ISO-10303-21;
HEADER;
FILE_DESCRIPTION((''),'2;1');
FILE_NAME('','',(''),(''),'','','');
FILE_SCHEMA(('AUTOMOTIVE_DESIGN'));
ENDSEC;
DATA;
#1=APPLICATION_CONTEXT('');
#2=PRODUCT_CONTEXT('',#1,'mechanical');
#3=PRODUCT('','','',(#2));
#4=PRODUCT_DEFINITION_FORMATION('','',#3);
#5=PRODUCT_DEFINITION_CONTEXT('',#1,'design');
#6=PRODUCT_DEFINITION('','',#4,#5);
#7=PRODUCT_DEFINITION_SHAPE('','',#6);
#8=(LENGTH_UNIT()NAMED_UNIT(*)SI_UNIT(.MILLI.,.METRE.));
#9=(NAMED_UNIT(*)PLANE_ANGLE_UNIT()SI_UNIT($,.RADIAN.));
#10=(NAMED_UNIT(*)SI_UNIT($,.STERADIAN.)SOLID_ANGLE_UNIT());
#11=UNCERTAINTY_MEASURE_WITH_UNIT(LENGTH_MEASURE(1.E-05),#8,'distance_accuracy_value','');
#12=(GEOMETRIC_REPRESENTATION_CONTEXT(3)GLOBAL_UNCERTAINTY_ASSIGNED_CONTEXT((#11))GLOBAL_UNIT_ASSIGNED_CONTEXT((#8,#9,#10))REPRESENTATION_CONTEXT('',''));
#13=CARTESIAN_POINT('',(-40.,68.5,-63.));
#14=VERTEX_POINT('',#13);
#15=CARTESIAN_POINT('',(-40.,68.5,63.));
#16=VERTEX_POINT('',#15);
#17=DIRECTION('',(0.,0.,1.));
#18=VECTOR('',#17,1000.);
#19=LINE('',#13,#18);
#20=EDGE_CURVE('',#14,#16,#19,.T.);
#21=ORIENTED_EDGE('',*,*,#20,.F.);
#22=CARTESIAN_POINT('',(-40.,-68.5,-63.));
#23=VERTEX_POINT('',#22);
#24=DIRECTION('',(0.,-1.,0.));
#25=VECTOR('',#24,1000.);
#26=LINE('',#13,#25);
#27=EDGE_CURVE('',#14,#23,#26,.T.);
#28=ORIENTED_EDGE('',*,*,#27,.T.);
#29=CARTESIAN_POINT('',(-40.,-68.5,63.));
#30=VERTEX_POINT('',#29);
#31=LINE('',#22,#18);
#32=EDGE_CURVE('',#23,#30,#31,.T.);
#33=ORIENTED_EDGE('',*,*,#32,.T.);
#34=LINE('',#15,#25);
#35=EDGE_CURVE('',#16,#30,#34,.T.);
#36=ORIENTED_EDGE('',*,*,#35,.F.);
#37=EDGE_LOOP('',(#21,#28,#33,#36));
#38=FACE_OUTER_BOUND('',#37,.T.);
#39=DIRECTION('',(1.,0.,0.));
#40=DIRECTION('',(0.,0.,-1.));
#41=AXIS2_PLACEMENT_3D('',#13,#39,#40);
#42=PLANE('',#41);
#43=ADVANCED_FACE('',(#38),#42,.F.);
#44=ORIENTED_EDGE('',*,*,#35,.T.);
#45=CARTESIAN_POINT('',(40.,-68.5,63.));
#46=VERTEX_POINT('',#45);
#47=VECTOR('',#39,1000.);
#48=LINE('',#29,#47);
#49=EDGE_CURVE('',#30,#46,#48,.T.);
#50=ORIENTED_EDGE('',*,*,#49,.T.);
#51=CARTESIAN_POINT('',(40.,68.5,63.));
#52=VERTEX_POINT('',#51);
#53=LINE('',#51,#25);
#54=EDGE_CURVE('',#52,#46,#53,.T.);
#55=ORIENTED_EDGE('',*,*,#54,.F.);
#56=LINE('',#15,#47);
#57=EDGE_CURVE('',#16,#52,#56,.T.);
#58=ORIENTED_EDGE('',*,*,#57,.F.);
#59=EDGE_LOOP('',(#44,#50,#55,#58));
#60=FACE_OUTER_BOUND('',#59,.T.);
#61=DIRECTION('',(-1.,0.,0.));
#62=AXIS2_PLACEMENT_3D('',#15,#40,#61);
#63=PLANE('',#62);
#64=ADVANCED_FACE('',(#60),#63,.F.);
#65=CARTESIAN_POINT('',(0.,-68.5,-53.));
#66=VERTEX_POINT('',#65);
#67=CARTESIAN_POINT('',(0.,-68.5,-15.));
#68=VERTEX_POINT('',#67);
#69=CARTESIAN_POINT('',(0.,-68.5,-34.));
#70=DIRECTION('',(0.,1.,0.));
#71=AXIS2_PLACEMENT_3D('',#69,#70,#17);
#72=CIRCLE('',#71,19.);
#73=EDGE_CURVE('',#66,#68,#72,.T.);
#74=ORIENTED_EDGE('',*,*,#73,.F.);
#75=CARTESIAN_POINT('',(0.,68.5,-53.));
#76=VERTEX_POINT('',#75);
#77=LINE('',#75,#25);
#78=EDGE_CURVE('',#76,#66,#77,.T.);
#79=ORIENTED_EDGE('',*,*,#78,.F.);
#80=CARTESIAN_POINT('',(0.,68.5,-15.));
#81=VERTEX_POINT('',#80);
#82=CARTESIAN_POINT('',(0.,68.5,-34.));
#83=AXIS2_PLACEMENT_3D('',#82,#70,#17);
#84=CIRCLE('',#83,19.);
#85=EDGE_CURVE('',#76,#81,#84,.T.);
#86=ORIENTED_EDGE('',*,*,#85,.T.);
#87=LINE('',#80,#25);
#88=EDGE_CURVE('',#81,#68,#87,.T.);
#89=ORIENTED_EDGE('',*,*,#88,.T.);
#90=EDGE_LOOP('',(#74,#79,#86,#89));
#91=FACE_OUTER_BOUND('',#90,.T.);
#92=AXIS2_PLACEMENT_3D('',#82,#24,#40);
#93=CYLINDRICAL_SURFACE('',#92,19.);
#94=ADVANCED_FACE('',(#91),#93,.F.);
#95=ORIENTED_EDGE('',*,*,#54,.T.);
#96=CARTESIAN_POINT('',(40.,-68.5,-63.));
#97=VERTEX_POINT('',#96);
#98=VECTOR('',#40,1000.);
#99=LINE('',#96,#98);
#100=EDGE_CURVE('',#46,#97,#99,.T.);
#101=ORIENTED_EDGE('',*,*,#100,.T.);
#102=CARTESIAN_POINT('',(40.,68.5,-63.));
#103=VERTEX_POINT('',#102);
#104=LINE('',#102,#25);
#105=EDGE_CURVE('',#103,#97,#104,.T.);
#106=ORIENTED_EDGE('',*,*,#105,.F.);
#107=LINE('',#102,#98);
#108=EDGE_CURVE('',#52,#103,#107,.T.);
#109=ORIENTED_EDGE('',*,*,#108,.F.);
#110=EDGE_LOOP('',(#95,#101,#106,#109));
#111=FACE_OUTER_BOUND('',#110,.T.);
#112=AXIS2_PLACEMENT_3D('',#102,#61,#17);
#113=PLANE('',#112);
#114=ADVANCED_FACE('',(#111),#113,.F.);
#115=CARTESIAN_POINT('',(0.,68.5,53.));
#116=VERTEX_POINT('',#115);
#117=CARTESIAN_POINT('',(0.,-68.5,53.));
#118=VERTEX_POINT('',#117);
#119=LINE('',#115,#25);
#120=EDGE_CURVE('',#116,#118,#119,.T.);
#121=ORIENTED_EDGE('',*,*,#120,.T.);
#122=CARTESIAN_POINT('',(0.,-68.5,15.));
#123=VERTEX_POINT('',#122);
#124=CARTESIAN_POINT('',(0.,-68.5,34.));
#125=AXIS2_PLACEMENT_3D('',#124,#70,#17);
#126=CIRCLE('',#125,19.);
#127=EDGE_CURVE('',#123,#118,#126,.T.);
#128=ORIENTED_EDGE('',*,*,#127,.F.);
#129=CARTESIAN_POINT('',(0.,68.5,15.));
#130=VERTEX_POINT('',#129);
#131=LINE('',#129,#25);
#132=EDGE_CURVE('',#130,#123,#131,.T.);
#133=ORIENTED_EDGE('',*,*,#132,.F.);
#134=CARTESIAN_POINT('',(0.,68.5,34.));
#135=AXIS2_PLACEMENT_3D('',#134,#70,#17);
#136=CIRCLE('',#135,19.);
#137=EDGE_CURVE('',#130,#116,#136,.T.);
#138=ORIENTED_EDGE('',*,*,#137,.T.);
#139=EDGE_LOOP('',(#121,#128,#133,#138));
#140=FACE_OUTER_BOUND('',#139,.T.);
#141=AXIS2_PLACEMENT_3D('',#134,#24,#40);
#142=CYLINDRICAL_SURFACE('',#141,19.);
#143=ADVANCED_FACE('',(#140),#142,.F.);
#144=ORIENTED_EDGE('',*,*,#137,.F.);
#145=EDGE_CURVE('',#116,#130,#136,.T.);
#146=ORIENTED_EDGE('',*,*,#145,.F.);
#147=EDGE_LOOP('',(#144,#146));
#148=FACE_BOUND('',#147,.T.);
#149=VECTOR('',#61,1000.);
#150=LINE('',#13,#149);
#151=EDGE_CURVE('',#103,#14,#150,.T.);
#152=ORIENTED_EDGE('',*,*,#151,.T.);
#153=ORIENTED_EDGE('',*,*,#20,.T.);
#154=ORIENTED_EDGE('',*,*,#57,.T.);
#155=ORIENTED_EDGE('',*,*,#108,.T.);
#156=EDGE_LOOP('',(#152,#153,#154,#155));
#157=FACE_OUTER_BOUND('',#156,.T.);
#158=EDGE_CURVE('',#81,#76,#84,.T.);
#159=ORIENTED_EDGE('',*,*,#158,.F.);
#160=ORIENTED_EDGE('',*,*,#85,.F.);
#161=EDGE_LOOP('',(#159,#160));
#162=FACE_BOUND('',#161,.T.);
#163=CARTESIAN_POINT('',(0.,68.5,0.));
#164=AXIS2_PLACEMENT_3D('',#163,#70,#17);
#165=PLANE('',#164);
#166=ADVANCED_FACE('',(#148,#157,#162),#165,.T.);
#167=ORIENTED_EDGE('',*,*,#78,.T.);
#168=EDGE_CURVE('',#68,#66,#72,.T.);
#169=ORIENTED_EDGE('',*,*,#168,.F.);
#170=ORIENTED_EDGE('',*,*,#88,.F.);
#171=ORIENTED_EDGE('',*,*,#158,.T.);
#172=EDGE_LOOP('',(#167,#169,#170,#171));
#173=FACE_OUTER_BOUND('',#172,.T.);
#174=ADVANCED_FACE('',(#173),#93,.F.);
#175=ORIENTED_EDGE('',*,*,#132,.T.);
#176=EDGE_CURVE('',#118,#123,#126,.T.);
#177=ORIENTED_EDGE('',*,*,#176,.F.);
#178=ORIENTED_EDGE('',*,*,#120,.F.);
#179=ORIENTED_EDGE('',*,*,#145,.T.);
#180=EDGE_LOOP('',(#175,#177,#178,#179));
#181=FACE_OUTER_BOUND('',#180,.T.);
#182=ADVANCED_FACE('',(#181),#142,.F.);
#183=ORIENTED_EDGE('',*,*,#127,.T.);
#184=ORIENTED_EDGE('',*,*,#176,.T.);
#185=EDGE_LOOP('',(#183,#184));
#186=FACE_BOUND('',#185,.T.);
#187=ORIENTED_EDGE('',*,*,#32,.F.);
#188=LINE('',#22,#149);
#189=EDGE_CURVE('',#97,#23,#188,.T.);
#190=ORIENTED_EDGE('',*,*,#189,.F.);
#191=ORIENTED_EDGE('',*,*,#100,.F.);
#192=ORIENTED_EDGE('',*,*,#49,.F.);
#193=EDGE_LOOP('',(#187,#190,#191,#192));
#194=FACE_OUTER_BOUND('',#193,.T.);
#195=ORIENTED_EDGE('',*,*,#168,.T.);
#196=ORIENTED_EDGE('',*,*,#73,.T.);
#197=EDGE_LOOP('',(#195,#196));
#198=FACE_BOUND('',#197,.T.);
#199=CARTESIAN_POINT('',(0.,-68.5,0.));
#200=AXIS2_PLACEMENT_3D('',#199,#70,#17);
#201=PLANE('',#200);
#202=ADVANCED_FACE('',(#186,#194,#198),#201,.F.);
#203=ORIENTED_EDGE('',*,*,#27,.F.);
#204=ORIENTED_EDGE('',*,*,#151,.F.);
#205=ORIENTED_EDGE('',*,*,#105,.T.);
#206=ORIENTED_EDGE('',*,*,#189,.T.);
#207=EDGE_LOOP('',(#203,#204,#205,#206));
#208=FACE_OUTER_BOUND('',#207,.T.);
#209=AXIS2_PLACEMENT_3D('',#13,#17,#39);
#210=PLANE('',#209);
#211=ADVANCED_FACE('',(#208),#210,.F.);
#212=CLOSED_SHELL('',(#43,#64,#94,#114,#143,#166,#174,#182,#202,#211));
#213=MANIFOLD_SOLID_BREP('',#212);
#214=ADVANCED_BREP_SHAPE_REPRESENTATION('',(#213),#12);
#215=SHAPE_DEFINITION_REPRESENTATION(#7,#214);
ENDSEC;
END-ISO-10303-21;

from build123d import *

# Parameters (mm, degrees)
SKETCH2_W           = 80
SKETCH2_H           = 126
SKETCH2_R           = 19
BOSS_EXTRUDE1_DEPTH = 68.5


with BuildPart() as part:
    # Sketch2 → Boss-Extrude1 (new, symmetric)
    with BuildSketch(Plane(origin=(0, 0, 0), x_dir=(1, 0, 0), z_dir=(0, 1, 0))):
        Rectangle(SKETCH2_W, SKETCH2_H)
        with Locations(Location((0, 34, 0), (0, 0, 270))):
            Circle(SKETCH2_R, mode=Mode.SUBTRACT)
        with Locations(Location((0, -34, 0), (0, 0, 270))):
            Circle(SKETCH2_R, mode=Mode.SUBTRACT)
    extrude(amount=BOSS_EXTRUDE1_DEPTH, both=True)


solid = part.part
